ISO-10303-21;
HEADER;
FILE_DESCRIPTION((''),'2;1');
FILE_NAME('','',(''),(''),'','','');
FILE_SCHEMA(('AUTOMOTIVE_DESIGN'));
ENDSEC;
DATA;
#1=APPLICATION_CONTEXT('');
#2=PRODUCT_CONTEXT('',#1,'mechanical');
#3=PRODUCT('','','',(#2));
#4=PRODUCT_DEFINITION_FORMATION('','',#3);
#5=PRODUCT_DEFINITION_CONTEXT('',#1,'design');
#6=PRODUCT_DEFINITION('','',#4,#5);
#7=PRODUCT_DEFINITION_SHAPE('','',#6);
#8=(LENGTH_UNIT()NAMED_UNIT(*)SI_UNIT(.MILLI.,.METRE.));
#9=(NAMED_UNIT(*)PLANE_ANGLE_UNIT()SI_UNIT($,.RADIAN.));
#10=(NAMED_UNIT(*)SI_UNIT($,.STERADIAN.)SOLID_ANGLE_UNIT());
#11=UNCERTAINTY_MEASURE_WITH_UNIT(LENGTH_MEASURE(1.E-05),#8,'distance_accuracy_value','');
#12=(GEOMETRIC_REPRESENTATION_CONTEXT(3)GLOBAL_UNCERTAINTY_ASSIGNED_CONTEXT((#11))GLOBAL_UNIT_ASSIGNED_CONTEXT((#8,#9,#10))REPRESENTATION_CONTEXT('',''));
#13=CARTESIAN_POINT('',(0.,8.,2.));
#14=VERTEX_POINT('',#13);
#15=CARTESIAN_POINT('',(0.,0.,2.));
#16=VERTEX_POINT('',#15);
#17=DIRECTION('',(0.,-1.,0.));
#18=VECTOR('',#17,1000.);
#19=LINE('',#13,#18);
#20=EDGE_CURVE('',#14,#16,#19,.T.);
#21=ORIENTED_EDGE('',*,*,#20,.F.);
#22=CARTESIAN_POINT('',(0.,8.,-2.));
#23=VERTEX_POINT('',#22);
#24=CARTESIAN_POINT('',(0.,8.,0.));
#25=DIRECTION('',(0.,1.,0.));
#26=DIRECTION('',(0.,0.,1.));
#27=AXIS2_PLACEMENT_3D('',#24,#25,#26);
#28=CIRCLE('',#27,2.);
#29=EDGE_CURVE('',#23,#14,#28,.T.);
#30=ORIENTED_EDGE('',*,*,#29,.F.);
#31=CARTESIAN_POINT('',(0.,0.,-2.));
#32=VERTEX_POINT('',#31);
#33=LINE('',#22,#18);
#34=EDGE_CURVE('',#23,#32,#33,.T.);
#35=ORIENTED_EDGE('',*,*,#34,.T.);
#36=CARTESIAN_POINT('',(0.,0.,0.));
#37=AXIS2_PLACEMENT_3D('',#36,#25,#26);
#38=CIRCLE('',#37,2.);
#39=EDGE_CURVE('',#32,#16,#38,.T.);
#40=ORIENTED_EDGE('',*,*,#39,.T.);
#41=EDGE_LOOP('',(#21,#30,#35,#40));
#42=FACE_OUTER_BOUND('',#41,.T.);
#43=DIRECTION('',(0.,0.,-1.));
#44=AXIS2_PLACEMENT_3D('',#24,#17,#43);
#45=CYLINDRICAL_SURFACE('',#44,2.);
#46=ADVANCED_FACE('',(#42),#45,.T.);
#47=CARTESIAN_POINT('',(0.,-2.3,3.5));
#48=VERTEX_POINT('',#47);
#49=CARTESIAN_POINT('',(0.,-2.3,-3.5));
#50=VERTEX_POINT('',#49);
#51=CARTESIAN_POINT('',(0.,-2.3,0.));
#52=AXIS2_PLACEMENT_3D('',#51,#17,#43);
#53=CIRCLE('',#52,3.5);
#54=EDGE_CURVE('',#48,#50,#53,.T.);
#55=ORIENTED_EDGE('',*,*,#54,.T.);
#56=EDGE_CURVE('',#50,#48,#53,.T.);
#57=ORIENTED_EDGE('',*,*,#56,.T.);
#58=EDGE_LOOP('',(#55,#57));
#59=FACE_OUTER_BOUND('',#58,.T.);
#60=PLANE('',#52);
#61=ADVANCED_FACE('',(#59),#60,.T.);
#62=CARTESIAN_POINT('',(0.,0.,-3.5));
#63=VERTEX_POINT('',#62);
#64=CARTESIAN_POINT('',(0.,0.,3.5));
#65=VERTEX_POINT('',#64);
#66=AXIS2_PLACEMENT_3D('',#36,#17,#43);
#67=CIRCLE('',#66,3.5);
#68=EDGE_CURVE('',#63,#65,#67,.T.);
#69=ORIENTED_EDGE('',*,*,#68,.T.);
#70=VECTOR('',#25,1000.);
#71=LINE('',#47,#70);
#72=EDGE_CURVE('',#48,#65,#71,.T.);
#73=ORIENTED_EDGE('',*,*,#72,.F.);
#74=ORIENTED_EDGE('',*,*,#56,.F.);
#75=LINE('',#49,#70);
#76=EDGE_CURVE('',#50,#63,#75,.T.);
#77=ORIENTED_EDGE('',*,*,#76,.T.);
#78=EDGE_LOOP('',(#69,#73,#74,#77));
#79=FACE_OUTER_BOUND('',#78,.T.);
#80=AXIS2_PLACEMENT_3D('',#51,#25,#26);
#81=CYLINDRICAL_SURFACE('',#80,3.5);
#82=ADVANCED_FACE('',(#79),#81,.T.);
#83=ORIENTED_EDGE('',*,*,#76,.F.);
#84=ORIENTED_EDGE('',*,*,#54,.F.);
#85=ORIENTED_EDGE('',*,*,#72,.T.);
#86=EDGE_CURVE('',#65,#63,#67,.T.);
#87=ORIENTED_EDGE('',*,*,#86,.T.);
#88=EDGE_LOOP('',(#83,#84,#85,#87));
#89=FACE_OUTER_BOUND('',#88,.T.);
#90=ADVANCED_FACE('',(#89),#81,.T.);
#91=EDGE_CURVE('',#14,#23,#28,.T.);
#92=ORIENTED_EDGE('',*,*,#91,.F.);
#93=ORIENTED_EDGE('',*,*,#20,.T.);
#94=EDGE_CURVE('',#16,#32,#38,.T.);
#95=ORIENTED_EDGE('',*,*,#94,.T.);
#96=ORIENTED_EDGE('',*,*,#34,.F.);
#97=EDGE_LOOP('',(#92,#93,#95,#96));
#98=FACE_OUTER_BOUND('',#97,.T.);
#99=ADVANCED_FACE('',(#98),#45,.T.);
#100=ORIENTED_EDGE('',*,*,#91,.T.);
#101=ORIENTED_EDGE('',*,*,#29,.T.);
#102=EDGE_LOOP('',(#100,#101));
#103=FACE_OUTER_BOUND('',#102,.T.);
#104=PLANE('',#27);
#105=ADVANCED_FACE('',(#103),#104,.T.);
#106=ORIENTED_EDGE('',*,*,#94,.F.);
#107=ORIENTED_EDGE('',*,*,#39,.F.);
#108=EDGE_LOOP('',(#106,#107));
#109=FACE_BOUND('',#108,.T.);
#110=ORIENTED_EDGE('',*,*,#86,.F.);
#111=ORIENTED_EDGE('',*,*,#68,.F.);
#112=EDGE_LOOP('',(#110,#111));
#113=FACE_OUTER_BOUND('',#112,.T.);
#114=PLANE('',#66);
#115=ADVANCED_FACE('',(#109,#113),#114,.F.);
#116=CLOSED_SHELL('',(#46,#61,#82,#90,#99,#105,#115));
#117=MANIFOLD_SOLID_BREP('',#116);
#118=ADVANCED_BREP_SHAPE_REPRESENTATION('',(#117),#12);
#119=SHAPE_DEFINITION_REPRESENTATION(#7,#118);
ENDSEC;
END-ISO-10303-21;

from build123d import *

# Parameters (mm, degrees)
SKETCH_1_R      = 2
EXTRUDE_1_DEPTH = 8
SKETCH_2_R      = 3.5
EXTRUDE_2_DEPTH = 2.3


with BuildPart() as part:
    # 草图1 → 凸台-拉伸1 (new body)
    with BuildSketch(Plane(origin=(0, 0, 0), x_dir=(1, 0, 0), z_dir=(0, 1, 0))):
        with Locations(Location((0, 0, 0), (0, 0, 270))):
            Circle(SKETCH_1_R)
    extrude(amount=EXTRUDE_1_DEPTH)

    # 草图2 → 凸台-拉伸2 (add)
    with BuildSketch(Plane.XZ):
        with Locations(Location((0, 0, 0), (0, 0, 270))):
            Circle(SKETCH_2_R)
    extrude(amount=EXTRUDE_2_DEPTH)


solid = part.part
